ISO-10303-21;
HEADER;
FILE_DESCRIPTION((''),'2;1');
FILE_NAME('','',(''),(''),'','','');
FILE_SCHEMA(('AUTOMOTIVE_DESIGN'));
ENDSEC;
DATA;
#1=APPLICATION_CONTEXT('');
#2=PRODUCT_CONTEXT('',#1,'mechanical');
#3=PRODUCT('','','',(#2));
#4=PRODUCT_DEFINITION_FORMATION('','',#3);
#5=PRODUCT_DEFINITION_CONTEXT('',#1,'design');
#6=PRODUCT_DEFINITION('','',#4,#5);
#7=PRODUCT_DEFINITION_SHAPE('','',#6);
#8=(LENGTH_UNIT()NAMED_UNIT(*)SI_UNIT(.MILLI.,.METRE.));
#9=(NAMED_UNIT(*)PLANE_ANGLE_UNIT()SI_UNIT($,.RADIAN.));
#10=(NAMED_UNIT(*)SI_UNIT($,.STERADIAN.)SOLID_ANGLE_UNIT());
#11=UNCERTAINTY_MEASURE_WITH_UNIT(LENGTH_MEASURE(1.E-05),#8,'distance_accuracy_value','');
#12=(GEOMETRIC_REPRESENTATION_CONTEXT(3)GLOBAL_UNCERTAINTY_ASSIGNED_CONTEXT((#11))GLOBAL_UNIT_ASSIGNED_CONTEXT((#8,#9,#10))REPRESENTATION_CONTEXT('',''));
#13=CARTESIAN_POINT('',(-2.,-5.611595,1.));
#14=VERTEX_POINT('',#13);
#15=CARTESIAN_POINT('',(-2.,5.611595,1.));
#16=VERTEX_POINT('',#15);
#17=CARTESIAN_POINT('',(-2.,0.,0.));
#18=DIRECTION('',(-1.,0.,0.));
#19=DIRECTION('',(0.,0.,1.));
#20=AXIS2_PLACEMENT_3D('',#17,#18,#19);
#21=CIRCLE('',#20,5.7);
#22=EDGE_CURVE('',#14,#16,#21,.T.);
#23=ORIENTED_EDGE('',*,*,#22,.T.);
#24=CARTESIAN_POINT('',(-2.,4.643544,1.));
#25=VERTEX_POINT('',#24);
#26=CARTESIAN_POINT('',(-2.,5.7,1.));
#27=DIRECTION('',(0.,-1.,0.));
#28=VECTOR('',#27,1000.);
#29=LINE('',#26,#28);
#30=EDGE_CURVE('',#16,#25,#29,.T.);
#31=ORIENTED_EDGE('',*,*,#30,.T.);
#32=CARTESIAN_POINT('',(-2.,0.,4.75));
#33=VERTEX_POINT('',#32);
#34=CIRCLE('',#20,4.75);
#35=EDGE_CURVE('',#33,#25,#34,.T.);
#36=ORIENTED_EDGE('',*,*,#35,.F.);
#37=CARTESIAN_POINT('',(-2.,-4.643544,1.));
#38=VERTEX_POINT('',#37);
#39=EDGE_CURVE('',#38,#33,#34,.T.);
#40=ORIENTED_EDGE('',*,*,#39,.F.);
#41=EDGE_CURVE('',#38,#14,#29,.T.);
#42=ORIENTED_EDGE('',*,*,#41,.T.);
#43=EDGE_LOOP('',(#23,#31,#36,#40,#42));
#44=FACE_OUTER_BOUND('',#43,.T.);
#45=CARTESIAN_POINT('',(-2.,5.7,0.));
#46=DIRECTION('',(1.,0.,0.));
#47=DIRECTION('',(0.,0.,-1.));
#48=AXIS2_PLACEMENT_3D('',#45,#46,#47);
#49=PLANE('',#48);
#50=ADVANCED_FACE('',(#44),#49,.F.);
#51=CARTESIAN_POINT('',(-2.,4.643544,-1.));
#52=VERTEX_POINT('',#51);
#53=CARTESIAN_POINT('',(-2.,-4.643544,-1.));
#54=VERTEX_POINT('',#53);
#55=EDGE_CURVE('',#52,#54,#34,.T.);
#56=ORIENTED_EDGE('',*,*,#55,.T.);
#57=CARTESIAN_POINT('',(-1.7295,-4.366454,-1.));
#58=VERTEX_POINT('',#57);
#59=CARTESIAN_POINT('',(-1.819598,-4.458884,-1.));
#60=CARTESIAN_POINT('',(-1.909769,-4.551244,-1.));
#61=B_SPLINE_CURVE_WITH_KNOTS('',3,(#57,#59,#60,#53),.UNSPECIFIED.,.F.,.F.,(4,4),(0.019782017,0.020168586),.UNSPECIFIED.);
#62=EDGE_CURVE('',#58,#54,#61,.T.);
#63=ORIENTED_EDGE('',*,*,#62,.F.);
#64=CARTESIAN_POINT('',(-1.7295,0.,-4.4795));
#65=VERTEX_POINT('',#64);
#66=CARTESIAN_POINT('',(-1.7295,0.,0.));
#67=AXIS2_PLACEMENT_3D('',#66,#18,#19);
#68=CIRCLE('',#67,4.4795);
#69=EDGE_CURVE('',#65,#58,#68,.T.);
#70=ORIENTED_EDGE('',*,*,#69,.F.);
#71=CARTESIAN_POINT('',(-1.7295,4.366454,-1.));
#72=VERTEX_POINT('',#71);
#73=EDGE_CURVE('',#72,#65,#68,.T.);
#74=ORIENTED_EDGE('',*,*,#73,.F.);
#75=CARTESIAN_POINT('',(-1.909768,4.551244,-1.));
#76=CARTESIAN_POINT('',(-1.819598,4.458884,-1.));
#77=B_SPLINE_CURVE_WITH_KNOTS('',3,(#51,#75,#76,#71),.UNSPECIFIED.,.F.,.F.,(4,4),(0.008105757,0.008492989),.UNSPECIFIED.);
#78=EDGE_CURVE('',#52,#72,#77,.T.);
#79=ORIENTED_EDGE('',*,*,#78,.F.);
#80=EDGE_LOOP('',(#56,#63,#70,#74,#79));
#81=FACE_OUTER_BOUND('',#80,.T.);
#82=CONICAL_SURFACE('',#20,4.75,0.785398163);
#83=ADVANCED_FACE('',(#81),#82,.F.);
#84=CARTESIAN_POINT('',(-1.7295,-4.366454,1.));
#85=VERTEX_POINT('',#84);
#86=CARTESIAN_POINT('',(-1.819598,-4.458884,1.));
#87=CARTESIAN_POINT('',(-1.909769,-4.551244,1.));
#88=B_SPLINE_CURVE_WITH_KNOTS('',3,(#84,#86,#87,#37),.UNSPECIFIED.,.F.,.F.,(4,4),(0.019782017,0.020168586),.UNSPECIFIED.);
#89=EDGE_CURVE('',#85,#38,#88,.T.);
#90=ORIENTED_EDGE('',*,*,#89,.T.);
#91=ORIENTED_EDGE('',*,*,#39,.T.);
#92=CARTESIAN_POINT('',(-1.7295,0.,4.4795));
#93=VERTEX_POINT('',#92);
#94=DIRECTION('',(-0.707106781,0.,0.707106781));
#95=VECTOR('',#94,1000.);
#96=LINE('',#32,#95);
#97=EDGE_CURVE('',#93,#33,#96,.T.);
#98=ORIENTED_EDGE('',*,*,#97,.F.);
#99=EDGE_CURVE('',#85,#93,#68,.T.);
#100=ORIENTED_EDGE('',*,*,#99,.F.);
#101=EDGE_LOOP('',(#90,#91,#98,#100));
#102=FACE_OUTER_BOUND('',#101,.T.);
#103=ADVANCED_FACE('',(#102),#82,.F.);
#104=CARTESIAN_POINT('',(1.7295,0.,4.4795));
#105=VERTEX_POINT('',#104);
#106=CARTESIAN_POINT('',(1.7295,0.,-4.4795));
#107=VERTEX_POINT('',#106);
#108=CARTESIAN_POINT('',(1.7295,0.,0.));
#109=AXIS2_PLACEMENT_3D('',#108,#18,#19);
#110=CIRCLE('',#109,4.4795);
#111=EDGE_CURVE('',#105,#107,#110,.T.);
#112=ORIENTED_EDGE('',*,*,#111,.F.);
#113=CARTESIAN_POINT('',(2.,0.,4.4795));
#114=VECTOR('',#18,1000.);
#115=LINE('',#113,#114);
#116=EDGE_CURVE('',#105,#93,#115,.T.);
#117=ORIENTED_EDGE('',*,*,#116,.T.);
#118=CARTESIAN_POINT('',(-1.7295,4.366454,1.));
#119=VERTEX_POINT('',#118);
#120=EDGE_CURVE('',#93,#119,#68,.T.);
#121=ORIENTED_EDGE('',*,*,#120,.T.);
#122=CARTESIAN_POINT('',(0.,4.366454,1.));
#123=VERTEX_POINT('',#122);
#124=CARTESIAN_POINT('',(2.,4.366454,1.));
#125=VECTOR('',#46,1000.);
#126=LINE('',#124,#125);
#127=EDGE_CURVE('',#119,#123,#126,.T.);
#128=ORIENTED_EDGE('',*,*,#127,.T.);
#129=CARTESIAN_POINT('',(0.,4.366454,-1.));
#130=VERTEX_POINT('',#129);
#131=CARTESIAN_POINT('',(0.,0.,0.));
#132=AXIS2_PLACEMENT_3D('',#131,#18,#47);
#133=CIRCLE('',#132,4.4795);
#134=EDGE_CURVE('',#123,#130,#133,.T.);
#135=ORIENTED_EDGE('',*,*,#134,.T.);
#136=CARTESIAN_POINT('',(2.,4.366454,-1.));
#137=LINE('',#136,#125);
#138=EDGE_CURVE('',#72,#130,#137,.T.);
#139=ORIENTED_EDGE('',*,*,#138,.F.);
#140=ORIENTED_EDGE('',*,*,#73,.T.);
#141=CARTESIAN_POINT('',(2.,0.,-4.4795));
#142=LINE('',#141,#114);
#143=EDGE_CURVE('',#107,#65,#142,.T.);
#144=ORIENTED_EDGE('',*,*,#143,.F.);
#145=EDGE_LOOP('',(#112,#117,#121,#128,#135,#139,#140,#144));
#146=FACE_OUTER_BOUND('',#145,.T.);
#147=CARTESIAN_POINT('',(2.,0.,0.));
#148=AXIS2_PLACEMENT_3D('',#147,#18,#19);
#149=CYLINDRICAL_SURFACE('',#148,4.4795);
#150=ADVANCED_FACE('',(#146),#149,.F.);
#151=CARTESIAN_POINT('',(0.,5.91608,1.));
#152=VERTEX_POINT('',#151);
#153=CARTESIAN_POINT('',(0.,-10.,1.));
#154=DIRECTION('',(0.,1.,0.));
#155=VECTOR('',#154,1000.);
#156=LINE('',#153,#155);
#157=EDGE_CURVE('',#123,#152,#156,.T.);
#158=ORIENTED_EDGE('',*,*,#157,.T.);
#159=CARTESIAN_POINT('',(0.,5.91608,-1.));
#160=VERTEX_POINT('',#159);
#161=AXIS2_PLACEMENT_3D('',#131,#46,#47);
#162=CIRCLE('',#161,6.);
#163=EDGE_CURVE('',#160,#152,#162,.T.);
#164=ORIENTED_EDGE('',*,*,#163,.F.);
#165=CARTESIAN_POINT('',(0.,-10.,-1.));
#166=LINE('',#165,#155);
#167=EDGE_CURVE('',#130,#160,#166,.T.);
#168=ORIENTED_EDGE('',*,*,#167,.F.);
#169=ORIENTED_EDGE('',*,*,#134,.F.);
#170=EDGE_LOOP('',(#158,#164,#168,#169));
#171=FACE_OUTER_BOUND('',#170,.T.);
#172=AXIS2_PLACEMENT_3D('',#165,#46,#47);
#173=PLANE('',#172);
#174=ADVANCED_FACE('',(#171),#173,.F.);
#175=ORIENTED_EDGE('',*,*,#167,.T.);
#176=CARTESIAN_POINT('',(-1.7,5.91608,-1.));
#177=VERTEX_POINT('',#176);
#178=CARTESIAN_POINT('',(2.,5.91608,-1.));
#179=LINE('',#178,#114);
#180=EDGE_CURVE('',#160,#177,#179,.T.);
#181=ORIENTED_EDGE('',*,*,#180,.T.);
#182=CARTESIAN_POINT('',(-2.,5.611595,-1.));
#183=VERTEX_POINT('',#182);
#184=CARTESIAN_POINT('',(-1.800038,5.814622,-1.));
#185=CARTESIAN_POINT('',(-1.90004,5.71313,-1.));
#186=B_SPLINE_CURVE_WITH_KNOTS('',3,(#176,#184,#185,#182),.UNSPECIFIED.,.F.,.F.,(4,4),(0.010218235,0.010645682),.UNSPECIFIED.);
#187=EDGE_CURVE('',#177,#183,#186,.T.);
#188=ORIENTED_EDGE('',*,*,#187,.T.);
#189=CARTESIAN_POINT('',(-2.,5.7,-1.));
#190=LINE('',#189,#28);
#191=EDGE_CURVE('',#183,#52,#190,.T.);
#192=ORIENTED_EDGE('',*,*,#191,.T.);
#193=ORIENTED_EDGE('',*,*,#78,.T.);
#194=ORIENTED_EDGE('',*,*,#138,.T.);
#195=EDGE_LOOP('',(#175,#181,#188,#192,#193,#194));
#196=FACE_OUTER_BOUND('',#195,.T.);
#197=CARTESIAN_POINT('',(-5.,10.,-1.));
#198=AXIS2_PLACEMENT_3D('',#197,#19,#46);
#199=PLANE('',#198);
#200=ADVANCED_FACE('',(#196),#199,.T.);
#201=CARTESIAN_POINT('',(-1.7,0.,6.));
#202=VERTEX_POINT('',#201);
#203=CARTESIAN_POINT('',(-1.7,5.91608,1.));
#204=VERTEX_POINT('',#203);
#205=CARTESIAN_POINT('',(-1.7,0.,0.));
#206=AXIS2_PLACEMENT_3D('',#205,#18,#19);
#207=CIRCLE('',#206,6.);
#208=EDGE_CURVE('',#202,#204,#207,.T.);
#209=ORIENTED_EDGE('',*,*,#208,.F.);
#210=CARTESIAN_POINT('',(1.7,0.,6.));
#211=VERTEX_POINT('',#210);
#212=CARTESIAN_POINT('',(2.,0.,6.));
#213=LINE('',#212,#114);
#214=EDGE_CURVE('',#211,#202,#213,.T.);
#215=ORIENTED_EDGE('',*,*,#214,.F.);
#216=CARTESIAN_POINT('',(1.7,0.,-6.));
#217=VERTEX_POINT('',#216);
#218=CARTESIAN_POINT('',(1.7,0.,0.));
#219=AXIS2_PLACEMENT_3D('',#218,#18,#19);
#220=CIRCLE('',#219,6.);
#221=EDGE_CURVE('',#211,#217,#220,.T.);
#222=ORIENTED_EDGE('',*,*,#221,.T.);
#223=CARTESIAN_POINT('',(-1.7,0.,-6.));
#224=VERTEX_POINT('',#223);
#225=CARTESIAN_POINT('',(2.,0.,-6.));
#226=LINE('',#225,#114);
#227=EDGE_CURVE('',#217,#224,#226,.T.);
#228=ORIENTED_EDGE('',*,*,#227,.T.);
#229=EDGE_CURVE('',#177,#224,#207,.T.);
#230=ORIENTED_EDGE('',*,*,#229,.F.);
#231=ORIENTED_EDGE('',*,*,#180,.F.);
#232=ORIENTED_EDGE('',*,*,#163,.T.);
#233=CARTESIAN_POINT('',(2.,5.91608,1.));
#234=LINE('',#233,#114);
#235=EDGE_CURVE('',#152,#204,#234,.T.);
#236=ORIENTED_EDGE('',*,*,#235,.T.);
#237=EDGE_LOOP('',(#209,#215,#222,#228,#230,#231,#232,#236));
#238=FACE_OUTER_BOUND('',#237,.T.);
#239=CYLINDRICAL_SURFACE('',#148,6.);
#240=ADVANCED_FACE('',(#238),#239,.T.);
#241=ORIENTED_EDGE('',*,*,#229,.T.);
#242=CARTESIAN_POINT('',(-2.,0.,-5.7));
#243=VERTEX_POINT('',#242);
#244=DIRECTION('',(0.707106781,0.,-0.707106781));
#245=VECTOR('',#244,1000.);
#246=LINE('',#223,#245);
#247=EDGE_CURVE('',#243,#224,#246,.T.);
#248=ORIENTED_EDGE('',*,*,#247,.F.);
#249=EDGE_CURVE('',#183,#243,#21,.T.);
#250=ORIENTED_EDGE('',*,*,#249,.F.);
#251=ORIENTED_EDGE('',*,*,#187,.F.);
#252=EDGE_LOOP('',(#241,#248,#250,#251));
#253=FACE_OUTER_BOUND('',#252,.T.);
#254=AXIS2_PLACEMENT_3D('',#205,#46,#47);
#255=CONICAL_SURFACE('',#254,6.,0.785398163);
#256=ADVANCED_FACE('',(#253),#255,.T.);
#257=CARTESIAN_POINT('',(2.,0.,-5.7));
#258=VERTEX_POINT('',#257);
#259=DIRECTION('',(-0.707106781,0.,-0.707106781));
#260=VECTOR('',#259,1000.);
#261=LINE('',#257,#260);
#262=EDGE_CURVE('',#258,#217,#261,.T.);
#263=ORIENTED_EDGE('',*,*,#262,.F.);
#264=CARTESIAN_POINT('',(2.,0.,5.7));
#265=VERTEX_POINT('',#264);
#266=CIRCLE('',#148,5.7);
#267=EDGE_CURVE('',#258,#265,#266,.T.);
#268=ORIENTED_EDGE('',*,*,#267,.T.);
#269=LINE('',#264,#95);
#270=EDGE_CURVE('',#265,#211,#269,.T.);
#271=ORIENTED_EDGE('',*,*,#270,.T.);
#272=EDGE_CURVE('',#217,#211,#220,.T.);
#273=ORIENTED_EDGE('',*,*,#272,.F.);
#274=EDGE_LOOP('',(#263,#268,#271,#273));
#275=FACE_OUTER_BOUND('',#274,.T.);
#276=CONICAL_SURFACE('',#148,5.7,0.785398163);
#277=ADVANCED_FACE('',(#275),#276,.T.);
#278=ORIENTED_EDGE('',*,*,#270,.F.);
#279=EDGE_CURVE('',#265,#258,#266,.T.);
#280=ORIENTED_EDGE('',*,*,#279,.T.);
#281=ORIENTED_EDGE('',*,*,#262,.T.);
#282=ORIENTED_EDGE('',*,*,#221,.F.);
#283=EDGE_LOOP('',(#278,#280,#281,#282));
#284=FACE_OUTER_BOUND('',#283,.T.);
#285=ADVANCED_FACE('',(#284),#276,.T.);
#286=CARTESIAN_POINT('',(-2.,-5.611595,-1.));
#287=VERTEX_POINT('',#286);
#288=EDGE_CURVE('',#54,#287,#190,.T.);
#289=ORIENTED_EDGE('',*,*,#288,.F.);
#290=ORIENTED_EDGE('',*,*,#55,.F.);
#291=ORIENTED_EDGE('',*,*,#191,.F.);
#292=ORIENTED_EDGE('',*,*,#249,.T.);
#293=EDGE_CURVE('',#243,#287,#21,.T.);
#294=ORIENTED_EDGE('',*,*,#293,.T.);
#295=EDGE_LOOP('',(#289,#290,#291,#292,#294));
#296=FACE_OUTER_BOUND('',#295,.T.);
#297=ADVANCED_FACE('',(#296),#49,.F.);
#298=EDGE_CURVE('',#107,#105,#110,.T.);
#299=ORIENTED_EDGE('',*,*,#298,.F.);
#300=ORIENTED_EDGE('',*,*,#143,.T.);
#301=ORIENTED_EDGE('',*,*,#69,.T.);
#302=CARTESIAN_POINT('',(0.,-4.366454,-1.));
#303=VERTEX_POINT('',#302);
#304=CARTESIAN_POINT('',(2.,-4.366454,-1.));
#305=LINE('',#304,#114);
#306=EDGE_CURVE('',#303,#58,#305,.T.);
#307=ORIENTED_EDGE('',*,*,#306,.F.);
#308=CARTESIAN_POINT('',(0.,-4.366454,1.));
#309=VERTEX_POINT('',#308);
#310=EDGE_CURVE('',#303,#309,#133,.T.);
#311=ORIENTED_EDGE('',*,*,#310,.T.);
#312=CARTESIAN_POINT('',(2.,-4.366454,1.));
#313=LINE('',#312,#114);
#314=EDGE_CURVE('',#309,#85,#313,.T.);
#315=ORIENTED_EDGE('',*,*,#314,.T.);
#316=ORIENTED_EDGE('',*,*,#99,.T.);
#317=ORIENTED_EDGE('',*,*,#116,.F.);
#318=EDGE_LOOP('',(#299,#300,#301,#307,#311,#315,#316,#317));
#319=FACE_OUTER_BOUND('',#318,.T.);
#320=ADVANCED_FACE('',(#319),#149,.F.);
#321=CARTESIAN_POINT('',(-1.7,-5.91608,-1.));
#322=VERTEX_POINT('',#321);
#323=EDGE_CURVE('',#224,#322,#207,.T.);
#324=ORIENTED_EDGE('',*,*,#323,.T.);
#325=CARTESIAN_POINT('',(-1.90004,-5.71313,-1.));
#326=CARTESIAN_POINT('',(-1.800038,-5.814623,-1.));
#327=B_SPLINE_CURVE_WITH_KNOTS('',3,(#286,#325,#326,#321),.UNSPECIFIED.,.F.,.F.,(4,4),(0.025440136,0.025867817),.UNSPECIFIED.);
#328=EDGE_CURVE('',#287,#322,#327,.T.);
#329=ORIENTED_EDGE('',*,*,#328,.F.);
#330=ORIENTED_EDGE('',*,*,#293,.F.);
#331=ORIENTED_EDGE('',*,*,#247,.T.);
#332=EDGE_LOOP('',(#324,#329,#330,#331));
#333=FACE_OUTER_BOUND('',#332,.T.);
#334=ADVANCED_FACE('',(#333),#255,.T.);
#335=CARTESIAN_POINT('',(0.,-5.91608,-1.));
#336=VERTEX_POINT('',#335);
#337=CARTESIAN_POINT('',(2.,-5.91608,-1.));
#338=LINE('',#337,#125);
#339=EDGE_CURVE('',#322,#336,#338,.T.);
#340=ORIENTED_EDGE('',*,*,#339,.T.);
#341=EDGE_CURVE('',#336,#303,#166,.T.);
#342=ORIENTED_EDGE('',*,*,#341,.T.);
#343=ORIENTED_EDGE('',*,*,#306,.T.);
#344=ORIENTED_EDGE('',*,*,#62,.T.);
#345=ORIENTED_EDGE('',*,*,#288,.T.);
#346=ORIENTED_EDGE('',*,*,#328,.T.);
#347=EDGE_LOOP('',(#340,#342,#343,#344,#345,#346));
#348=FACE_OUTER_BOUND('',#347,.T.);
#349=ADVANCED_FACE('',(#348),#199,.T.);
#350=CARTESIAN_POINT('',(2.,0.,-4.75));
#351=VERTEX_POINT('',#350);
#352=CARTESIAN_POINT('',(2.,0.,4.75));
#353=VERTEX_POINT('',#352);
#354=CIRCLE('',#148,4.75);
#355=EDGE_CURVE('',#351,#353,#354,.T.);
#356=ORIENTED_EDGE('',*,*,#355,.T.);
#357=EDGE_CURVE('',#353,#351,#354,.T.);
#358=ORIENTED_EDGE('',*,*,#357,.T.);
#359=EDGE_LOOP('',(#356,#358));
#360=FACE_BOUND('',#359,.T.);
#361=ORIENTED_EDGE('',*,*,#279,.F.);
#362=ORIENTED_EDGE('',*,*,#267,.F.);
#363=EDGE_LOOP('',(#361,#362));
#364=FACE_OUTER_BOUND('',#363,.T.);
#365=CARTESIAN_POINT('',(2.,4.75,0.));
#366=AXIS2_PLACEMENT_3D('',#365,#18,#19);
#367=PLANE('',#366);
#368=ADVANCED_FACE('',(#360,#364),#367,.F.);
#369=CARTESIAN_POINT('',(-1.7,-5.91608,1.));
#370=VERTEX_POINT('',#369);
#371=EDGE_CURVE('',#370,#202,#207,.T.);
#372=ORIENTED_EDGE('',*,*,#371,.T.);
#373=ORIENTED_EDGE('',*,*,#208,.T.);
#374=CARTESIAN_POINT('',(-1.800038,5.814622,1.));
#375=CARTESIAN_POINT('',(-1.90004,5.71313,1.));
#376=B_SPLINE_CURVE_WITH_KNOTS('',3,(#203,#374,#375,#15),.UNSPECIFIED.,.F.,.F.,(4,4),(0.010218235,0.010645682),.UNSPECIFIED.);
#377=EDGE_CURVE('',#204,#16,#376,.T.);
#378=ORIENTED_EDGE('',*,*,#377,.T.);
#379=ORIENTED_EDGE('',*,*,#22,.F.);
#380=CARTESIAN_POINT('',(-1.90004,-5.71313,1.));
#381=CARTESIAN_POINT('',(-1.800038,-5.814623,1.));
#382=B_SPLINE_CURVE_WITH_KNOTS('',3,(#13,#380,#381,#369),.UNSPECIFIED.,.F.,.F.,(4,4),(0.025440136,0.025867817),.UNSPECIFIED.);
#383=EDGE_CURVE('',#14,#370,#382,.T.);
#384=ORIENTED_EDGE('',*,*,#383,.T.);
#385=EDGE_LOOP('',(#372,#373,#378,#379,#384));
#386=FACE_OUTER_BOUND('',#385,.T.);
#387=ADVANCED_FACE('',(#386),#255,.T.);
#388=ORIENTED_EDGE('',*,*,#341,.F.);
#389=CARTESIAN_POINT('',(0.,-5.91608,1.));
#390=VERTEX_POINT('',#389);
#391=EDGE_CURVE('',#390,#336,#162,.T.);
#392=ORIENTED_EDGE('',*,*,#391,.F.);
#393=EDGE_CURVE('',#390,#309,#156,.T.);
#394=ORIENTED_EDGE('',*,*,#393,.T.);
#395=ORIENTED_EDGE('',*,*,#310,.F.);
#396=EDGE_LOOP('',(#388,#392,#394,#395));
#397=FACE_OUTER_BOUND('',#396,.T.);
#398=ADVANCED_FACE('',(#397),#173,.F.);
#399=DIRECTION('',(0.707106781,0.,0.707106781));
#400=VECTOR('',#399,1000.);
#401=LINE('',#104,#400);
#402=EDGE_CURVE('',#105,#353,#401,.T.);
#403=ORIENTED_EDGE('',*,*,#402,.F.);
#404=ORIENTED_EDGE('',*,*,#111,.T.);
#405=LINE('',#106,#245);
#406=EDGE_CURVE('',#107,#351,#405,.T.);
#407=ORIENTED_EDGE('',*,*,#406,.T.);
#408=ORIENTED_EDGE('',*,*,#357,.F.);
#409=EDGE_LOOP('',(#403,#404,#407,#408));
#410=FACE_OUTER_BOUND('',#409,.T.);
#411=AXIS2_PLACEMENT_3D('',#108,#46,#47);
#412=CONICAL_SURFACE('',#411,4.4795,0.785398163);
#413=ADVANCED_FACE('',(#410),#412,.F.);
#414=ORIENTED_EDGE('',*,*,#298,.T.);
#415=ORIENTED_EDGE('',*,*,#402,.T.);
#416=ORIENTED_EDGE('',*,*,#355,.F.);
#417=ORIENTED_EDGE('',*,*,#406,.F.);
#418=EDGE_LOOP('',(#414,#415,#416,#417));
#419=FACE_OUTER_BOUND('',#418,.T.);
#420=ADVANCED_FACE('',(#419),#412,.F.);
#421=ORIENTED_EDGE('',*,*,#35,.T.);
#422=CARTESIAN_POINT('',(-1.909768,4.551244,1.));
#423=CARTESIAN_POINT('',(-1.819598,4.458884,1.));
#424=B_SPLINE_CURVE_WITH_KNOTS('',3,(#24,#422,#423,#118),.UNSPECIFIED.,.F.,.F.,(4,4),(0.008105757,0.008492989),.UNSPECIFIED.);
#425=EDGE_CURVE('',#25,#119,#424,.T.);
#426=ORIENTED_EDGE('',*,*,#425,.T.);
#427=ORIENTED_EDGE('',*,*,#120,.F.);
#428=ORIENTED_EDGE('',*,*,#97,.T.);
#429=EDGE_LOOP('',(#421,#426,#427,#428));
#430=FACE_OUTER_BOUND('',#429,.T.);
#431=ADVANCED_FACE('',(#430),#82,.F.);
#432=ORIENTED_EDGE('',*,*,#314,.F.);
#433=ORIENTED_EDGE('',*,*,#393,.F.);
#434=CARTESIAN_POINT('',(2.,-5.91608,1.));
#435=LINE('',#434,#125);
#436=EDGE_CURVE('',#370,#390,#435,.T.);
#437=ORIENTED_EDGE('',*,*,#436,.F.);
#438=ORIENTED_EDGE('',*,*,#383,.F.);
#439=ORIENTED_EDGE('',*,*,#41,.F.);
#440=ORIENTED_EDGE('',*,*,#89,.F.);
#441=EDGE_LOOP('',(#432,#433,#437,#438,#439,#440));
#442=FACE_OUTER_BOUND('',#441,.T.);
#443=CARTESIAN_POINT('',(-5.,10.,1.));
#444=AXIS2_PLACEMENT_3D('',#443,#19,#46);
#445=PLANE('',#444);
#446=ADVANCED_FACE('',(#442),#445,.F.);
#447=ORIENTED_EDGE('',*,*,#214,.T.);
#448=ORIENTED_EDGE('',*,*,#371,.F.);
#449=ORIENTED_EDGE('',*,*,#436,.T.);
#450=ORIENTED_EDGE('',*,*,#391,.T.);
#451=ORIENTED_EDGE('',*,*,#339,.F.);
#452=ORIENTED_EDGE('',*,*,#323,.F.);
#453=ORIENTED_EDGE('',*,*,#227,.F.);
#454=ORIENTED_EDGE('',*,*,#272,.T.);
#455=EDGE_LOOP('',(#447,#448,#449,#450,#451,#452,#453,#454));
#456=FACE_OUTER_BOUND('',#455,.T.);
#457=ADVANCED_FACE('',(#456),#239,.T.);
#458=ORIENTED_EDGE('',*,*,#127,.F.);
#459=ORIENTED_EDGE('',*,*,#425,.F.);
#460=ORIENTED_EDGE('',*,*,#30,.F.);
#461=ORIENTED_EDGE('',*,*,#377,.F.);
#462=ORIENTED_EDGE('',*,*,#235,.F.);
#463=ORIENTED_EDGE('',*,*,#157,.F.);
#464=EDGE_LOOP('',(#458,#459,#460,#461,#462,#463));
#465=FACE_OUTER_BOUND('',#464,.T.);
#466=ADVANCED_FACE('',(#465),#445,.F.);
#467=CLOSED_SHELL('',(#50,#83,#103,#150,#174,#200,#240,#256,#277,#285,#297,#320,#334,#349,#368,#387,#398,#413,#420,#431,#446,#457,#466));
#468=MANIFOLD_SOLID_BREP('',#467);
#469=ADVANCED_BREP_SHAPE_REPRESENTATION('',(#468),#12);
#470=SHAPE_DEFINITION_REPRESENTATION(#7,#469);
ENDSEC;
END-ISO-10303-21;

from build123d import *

# Parameters (mm, degrees)
CUT_EXTRUDE1_DEPTH      = 1
CUT_EXTRUDE1_DEPTH_BACK = 1
SKETCH2_W               = 5
SKETCH2_H               = 20


with BuildPart() as part:
    # Sketch1 → Revolve1 (revolve)
    with BuildSketch(Plane.XY, mode=Mode.PRIVATE) as revolve1_sk:
        Polygon((-2, 5.7), (-2, 4.75), (-1.7295, 4.4795), (1.7295, 4.4795), (2, 4.75), (2, 5.7), (1.7, 6), (-1.7, 6), align=None)
    revolve(revolve1_sk.sketch.rotate(Axis((2, 0, 0), (-1, 0, 0)), 270), axis=Axis((2, 0, 0), (-1, 0, 0)))

    # Sketch2 → Cut-Extrude1 (cut, two sides: drawn at the far end of the back side and taken through both)
    with BuildSketch(Plane.XY.offset(-CUT_EXTRUDE1_DEPTH_BACK)):
        with Locations((-2.5, 0)):
            Rectangle(SKETCH2_W, SKETCH2_H)
    extrude(amount=CUT_EXTRUDE1_DEPTH + CUT_EXTRUDE1_DEPTH_BACK, mode=Mode.SUBTRACT)


solid = part.part
